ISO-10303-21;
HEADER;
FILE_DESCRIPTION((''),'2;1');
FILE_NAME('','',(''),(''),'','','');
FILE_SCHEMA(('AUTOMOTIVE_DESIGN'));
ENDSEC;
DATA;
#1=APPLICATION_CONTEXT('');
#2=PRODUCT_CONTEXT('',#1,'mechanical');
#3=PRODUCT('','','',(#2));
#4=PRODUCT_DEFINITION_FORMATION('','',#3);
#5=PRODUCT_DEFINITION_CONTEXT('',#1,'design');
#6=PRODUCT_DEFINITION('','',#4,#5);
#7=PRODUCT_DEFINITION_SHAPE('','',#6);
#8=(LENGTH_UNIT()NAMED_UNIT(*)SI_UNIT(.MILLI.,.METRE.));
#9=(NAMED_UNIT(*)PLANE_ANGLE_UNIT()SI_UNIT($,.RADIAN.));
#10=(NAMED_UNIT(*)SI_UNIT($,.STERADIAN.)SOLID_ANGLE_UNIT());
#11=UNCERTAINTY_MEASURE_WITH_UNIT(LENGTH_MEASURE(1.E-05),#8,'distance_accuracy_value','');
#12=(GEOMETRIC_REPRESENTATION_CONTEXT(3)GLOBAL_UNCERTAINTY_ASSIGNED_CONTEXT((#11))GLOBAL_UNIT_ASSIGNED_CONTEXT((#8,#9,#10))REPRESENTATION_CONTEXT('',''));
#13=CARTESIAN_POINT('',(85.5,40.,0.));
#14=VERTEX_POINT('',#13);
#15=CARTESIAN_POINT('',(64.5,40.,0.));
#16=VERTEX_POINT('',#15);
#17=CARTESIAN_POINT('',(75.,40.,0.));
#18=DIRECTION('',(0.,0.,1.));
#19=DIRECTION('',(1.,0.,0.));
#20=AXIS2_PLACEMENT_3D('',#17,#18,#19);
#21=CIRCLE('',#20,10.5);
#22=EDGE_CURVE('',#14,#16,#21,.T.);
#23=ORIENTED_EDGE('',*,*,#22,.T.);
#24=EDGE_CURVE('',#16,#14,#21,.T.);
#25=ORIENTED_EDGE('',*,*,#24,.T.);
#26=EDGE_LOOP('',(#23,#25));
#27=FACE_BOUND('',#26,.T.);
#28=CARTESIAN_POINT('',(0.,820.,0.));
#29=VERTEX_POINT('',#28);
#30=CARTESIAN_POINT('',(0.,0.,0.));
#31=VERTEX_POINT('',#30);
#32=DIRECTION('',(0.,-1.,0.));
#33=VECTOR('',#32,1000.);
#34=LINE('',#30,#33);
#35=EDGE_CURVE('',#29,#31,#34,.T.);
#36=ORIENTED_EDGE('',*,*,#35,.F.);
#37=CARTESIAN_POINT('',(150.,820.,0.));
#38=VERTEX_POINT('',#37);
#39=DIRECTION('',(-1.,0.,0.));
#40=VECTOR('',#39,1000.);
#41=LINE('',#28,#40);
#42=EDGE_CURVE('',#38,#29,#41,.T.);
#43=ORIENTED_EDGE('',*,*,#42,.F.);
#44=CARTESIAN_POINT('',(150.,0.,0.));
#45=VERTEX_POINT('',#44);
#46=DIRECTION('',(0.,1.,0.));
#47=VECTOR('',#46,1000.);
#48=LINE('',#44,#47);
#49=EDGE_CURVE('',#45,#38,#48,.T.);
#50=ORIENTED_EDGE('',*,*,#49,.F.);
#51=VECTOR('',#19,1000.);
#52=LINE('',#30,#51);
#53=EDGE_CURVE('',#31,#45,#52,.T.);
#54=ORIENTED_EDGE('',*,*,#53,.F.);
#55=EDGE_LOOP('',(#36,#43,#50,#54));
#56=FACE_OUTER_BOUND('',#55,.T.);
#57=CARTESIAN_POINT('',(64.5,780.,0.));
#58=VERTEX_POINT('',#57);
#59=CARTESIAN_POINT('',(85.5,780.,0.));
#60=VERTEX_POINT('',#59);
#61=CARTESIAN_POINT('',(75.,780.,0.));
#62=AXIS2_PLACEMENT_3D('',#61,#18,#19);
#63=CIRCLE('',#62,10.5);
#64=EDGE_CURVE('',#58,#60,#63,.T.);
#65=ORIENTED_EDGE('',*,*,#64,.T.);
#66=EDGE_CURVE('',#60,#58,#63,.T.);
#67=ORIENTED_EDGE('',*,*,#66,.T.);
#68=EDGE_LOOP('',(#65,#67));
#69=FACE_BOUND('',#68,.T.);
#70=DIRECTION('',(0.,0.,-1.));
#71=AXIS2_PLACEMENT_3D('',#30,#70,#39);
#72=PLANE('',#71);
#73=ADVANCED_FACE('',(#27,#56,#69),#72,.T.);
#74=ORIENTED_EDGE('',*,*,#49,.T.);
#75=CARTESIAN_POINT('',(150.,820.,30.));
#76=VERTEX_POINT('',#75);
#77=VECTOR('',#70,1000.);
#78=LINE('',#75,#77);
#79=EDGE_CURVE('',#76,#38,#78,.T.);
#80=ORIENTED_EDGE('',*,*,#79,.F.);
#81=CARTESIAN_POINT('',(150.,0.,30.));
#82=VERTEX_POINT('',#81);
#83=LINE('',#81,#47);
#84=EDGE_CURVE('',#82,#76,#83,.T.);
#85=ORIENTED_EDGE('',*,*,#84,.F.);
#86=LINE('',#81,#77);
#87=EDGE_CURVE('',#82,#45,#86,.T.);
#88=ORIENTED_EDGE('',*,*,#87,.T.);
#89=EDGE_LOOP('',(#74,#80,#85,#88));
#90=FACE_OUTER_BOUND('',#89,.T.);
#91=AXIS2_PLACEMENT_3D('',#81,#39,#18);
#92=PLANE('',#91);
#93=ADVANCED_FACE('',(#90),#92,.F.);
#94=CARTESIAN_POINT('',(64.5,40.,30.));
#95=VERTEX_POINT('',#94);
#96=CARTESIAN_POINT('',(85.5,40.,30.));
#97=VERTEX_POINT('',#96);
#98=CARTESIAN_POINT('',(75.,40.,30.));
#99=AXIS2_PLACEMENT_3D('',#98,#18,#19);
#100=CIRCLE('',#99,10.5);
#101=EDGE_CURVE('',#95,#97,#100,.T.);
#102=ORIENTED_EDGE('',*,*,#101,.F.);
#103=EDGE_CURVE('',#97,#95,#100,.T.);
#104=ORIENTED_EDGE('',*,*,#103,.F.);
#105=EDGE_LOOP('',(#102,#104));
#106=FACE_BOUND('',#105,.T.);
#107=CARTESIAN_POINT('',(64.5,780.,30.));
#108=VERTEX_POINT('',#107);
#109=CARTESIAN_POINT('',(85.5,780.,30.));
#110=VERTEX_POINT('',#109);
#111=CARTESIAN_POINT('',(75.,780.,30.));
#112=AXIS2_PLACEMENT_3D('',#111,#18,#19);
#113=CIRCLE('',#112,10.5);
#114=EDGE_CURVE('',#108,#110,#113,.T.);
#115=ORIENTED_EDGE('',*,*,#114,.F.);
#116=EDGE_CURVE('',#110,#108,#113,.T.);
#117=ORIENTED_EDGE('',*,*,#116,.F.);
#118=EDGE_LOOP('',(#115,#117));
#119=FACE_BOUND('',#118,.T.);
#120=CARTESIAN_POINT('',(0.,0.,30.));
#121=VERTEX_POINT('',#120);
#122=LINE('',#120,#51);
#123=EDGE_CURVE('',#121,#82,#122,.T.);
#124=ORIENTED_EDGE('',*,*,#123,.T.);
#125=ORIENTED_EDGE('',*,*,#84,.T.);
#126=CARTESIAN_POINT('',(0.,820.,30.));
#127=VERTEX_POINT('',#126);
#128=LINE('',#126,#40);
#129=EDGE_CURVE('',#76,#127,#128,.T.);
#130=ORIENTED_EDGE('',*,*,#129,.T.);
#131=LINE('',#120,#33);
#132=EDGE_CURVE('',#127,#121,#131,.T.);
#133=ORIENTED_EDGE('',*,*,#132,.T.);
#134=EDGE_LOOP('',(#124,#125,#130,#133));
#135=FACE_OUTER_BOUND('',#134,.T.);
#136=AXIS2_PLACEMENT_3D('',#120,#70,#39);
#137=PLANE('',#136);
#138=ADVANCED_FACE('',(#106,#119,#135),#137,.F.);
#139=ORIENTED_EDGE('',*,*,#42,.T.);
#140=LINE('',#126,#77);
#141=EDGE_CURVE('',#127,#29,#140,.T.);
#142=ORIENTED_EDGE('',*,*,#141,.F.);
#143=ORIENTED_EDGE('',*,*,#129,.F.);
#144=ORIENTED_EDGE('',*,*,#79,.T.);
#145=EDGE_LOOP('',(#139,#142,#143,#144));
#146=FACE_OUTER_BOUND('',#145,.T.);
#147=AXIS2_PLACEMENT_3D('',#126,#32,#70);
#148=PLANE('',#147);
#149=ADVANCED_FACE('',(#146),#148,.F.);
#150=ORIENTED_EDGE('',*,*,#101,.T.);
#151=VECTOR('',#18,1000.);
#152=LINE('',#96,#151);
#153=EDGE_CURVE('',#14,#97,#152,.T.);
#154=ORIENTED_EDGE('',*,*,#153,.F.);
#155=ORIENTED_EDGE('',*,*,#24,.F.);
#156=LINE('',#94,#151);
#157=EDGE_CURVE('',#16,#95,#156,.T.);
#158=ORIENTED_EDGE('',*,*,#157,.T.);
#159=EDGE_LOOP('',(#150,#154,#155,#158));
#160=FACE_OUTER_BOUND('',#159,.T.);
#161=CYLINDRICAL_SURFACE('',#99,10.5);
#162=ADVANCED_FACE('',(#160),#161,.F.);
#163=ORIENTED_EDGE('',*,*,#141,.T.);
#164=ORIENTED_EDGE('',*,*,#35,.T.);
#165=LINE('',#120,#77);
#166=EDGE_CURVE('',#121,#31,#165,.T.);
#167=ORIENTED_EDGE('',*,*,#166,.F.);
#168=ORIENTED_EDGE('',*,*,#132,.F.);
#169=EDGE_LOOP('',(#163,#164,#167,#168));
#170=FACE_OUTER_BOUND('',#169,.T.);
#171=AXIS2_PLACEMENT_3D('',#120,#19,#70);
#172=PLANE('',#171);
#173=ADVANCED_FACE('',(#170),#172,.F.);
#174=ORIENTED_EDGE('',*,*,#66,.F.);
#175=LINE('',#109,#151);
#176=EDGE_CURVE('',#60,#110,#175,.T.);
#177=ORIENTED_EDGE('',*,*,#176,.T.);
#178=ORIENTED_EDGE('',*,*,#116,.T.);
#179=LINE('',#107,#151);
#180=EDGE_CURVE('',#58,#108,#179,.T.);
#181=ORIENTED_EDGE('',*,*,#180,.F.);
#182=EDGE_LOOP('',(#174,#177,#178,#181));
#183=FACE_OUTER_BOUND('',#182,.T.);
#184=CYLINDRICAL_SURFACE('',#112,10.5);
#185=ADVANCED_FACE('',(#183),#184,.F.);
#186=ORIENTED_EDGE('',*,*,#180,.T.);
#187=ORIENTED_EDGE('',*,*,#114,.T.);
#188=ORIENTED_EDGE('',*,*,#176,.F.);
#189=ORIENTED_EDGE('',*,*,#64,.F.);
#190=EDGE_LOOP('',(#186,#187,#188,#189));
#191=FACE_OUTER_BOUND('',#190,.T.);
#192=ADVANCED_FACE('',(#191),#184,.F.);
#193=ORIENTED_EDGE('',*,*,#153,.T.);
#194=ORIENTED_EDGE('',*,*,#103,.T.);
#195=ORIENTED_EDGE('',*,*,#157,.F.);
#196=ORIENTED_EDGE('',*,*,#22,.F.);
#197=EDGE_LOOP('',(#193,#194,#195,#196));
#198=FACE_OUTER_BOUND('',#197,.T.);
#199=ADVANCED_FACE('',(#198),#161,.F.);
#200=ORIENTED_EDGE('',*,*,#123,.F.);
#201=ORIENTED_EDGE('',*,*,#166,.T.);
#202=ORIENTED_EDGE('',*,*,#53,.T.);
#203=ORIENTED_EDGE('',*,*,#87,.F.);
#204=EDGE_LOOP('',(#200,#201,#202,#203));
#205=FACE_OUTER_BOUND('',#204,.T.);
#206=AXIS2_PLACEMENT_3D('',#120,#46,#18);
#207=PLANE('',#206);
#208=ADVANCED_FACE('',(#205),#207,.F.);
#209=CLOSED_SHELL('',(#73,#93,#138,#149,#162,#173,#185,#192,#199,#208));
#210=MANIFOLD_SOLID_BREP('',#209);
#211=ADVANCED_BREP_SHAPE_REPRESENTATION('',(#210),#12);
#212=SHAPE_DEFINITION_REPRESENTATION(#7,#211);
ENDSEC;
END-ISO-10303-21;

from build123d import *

# Parameters (mm, degrees)
SKETCH1_W                      = 150
SKETCH1_H                      = 820
BOSS_EXTRUDE1_DEPTH            = 30
M24_THREADED_HOLE1_D           = 21
M24_THREADED_HOLE1_ON_FACE_2_D = 21


with BuildPart() as part:
    # Sketch1 → Boss-Extrude1 (new body)
    with BuildSketch(Plane.XY):
        with Locations((75, 410)):
            Rectangle(SKETCH1_W, SKETCH1_H)
    extrude(amount=BOSS_EXTRUDE1_DEPTH)

    # M24 Threaded hole1 (through all)
    with Locations(Plane(origin=(75, 780, 30), x_dir=(1, 0, 0), z_dir=(0, 0, 1))):
        with Locations((0, 0), (0, -740)):
            Hole(M24_THREADED_HOLE1_D / 2)

    # M24 Threaded hole1 on face 2 (through all)
    with Locations(Plane(origin=(283.451995804, 183.295208972, 0), x_dir=(1, 0, 0), z_dir=(0, 0, 1))):
        with Locations((0, 0)):
            Hole(M24_THREADED_HOLE1_ON_FACE_2_D / 2)


solid = part.part
